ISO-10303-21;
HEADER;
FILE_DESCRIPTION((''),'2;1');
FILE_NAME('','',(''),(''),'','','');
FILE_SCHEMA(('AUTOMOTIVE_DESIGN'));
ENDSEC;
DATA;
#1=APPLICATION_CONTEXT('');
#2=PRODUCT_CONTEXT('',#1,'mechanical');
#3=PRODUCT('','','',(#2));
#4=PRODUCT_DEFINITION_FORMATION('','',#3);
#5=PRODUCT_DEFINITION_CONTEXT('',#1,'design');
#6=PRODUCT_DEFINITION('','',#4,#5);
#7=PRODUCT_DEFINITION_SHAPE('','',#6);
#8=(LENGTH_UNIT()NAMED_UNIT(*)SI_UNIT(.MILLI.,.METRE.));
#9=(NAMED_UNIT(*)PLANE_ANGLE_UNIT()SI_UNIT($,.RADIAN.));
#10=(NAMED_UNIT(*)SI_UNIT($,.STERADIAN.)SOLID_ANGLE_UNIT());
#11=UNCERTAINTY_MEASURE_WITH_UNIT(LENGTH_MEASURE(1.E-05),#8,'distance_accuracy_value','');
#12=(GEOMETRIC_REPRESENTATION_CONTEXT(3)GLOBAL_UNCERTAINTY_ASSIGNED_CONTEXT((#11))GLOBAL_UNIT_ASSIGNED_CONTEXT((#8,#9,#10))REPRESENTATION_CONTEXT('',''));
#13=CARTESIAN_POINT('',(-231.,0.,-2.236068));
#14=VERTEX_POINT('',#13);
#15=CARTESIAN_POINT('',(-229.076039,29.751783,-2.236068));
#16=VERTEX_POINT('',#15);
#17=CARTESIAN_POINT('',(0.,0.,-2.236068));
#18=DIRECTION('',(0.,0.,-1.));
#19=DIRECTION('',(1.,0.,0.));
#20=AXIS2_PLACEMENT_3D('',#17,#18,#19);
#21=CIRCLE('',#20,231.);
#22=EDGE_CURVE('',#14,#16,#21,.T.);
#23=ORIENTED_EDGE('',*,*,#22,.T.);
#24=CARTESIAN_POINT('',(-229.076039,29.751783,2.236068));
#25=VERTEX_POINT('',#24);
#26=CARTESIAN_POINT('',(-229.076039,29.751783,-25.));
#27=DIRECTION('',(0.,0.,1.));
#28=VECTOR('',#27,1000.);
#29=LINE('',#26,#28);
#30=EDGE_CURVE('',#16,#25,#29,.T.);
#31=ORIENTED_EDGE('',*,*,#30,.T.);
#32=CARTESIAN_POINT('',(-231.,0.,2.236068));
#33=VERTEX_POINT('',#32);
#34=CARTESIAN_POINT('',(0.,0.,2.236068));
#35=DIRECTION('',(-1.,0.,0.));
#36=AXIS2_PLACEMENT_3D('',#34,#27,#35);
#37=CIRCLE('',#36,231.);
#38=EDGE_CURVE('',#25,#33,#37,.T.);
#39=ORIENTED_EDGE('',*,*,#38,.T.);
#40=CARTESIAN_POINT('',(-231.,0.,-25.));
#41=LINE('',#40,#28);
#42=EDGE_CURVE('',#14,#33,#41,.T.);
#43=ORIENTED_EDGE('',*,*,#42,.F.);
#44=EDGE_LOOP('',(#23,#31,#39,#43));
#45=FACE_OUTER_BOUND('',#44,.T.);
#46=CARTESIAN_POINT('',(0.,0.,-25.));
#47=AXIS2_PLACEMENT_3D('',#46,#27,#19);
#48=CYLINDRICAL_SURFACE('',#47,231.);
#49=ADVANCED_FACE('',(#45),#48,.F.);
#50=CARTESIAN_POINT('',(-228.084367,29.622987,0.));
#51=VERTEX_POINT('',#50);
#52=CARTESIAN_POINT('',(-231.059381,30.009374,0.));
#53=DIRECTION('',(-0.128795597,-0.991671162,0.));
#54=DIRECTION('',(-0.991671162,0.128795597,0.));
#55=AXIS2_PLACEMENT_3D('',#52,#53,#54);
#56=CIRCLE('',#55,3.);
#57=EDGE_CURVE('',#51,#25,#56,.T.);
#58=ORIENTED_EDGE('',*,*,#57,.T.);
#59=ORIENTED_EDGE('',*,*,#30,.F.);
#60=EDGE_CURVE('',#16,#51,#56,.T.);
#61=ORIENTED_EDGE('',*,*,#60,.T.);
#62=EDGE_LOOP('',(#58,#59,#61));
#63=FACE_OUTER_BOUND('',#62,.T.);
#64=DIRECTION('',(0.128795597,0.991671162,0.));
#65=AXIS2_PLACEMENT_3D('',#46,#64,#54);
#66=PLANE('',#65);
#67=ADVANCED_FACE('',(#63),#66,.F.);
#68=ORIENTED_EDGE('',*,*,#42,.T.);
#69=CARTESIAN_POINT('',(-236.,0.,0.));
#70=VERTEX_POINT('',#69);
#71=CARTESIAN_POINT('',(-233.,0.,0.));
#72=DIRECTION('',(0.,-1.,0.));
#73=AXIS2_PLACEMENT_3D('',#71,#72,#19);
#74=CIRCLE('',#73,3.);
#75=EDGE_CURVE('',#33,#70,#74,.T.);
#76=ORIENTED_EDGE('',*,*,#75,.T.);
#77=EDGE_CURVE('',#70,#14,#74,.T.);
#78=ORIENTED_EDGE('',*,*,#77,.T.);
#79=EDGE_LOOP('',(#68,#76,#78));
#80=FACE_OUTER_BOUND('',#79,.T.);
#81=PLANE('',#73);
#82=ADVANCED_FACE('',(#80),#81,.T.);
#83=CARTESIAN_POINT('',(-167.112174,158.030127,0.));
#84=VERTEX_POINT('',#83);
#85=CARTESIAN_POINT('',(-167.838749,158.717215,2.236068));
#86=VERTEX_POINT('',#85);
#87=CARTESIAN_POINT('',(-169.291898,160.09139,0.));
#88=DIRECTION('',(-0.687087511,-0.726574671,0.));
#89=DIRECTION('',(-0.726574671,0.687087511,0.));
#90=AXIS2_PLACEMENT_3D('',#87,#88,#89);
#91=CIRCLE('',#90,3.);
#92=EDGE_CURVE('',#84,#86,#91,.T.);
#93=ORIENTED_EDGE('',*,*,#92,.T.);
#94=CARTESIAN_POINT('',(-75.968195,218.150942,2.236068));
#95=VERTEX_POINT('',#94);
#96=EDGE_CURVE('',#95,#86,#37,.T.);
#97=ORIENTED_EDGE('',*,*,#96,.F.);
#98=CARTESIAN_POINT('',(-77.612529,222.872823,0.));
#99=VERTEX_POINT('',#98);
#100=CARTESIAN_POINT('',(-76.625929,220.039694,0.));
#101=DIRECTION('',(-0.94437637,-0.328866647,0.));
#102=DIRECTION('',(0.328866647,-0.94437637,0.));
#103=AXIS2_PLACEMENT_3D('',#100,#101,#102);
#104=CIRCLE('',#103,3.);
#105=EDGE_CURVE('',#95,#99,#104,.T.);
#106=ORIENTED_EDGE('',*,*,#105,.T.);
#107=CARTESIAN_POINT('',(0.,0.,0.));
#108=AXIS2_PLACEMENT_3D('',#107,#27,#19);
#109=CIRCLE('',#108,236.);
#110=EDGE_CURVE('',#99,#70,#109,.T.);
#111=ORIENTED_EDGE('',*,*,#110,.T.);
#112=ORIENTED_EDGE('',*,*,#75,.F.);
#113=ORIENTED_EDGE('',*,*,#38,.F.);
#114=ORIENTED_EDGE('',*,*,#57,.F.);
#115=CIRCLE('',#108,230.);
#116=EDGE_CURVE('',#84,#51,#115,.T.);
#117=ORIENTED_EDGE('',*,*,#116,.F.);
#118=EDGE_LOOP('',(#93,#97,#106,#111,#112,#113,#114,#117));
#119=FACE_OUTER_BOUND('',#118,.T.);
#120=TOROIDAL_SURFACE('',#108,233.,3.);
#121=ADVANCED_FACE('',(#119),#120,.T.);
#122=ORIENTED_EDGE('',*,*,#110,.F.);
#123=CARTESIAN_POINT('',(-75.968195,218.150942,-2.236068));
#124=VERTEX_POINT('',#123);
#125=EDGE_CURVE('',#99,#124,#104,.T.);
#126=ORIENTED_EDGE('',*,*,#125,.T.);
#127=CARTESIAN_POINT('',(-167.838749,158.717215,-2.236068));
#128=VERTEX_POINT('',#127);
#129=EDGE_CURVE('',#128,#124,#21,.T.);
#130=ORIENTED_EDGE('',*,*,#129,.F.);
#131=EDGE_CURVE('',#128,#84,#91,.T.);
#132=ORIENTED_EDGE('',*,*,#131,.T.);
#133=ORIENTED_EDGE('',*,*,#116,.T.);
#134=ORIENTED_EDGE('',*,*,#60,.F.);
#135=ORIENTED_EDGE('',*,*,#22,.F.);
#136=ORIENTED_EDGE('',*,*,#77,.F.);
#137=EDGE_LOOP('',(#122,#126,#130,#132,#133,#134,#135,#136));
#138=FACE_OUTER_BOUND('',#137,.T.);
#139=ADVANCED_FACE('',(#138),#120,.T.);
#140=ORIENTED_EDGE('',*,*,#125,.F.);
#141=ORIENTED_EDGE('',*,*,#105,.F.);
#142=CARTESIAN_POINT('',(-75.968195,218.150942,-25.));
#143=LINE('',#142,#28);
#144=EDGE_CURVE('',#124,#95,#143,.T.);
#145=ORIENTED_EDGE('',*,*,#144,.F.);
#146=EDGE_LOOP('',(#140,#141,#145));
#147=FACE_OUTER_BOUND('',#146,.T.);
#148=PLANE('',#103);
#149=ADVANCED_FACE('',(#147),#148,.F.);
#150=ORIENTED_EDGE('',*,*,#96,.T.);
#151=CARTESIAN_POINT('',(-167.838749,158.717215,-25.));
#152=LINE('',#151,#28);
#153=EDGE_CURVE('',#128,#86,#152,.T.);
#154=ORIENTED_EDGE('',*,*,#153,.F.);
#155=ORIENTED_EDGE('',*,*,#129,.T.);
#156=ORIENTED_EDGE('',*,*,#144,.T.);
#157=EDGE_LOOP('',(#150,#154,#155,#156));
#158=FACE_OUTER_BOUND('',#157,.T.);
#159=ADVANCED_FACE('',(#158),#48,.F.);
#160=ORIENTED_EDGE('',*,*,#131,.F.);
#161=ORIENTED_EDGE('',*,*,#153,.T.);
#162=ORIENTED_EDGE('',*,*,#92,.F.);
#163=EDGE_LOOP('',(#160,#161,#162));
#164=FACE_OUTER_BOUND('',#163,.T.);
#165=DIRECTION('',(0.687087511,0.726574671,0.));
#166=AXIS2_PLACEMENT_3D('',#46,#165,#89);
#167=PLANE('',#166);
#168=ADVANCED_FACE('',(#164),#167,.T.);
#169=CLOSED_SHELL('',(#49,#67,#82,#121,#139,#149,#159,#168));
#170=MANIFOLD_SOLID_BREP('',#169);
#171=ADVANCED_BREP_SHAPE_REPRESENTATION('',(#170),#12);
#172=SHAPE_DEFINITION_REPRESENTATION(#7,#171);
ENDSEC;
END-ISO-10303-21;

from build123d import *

# Parameters (mm, degrees)
SWEEP1_PROFILE_R   = 3
CUT_EXTRUDE1_DEPTH = 25


with BuildPart() as part:
    # Sweep1: sweep along a path in Sketch1
    with BuildLine(Plane.XY) as sweep1_path:
        ThreePointArc((-76.62592869, 220.039694265), (-189.924776405, 134.972513156), (-233, 0))
    # Sweep1 profile (on start of the path) → Sweep1 (sweep)
    with BuildSketch(Plane(origin=(-76.62592869, 220.039694265, 0), x_dir=(0.3288666467385807, -0.944376370237482, 0), z_dir=(-0.944376370237482, -0.3288666467385807, 0))):
        Circle(SWEEP1_PROFILE_R)
    sweep(path=sweep1_path.line)

    # Sketch6 → Cut-Extrude1 (cut, symmetric)
    with BuildSketch(Plane.XY):
        with BuildLine():
            Line((0, 0), (-229.07603851, 29.751782809))
            ThreePointArc((-229.07603851, 29.751782809), (-230.518507821, 14.906963206), (-231, 0))
            Line((-231, 0), (0, 0))
        make_face()
        with BuildLine():
            Line((0, 0), (-75.968195397, 218.150941525))
            ThreePointArc((-75.968195397, 218.150941525), (-125.473297939, 193.952188707), (-167.838748994, 158.717214996))
            Line((-167.838748994, 158.717214996), (0, 0))
        make_face()
    extrude(amount=CUT_EXTRUDE1_DEPTH, both=True, mode=Mode.SUBTRACT)


solid = part.part
